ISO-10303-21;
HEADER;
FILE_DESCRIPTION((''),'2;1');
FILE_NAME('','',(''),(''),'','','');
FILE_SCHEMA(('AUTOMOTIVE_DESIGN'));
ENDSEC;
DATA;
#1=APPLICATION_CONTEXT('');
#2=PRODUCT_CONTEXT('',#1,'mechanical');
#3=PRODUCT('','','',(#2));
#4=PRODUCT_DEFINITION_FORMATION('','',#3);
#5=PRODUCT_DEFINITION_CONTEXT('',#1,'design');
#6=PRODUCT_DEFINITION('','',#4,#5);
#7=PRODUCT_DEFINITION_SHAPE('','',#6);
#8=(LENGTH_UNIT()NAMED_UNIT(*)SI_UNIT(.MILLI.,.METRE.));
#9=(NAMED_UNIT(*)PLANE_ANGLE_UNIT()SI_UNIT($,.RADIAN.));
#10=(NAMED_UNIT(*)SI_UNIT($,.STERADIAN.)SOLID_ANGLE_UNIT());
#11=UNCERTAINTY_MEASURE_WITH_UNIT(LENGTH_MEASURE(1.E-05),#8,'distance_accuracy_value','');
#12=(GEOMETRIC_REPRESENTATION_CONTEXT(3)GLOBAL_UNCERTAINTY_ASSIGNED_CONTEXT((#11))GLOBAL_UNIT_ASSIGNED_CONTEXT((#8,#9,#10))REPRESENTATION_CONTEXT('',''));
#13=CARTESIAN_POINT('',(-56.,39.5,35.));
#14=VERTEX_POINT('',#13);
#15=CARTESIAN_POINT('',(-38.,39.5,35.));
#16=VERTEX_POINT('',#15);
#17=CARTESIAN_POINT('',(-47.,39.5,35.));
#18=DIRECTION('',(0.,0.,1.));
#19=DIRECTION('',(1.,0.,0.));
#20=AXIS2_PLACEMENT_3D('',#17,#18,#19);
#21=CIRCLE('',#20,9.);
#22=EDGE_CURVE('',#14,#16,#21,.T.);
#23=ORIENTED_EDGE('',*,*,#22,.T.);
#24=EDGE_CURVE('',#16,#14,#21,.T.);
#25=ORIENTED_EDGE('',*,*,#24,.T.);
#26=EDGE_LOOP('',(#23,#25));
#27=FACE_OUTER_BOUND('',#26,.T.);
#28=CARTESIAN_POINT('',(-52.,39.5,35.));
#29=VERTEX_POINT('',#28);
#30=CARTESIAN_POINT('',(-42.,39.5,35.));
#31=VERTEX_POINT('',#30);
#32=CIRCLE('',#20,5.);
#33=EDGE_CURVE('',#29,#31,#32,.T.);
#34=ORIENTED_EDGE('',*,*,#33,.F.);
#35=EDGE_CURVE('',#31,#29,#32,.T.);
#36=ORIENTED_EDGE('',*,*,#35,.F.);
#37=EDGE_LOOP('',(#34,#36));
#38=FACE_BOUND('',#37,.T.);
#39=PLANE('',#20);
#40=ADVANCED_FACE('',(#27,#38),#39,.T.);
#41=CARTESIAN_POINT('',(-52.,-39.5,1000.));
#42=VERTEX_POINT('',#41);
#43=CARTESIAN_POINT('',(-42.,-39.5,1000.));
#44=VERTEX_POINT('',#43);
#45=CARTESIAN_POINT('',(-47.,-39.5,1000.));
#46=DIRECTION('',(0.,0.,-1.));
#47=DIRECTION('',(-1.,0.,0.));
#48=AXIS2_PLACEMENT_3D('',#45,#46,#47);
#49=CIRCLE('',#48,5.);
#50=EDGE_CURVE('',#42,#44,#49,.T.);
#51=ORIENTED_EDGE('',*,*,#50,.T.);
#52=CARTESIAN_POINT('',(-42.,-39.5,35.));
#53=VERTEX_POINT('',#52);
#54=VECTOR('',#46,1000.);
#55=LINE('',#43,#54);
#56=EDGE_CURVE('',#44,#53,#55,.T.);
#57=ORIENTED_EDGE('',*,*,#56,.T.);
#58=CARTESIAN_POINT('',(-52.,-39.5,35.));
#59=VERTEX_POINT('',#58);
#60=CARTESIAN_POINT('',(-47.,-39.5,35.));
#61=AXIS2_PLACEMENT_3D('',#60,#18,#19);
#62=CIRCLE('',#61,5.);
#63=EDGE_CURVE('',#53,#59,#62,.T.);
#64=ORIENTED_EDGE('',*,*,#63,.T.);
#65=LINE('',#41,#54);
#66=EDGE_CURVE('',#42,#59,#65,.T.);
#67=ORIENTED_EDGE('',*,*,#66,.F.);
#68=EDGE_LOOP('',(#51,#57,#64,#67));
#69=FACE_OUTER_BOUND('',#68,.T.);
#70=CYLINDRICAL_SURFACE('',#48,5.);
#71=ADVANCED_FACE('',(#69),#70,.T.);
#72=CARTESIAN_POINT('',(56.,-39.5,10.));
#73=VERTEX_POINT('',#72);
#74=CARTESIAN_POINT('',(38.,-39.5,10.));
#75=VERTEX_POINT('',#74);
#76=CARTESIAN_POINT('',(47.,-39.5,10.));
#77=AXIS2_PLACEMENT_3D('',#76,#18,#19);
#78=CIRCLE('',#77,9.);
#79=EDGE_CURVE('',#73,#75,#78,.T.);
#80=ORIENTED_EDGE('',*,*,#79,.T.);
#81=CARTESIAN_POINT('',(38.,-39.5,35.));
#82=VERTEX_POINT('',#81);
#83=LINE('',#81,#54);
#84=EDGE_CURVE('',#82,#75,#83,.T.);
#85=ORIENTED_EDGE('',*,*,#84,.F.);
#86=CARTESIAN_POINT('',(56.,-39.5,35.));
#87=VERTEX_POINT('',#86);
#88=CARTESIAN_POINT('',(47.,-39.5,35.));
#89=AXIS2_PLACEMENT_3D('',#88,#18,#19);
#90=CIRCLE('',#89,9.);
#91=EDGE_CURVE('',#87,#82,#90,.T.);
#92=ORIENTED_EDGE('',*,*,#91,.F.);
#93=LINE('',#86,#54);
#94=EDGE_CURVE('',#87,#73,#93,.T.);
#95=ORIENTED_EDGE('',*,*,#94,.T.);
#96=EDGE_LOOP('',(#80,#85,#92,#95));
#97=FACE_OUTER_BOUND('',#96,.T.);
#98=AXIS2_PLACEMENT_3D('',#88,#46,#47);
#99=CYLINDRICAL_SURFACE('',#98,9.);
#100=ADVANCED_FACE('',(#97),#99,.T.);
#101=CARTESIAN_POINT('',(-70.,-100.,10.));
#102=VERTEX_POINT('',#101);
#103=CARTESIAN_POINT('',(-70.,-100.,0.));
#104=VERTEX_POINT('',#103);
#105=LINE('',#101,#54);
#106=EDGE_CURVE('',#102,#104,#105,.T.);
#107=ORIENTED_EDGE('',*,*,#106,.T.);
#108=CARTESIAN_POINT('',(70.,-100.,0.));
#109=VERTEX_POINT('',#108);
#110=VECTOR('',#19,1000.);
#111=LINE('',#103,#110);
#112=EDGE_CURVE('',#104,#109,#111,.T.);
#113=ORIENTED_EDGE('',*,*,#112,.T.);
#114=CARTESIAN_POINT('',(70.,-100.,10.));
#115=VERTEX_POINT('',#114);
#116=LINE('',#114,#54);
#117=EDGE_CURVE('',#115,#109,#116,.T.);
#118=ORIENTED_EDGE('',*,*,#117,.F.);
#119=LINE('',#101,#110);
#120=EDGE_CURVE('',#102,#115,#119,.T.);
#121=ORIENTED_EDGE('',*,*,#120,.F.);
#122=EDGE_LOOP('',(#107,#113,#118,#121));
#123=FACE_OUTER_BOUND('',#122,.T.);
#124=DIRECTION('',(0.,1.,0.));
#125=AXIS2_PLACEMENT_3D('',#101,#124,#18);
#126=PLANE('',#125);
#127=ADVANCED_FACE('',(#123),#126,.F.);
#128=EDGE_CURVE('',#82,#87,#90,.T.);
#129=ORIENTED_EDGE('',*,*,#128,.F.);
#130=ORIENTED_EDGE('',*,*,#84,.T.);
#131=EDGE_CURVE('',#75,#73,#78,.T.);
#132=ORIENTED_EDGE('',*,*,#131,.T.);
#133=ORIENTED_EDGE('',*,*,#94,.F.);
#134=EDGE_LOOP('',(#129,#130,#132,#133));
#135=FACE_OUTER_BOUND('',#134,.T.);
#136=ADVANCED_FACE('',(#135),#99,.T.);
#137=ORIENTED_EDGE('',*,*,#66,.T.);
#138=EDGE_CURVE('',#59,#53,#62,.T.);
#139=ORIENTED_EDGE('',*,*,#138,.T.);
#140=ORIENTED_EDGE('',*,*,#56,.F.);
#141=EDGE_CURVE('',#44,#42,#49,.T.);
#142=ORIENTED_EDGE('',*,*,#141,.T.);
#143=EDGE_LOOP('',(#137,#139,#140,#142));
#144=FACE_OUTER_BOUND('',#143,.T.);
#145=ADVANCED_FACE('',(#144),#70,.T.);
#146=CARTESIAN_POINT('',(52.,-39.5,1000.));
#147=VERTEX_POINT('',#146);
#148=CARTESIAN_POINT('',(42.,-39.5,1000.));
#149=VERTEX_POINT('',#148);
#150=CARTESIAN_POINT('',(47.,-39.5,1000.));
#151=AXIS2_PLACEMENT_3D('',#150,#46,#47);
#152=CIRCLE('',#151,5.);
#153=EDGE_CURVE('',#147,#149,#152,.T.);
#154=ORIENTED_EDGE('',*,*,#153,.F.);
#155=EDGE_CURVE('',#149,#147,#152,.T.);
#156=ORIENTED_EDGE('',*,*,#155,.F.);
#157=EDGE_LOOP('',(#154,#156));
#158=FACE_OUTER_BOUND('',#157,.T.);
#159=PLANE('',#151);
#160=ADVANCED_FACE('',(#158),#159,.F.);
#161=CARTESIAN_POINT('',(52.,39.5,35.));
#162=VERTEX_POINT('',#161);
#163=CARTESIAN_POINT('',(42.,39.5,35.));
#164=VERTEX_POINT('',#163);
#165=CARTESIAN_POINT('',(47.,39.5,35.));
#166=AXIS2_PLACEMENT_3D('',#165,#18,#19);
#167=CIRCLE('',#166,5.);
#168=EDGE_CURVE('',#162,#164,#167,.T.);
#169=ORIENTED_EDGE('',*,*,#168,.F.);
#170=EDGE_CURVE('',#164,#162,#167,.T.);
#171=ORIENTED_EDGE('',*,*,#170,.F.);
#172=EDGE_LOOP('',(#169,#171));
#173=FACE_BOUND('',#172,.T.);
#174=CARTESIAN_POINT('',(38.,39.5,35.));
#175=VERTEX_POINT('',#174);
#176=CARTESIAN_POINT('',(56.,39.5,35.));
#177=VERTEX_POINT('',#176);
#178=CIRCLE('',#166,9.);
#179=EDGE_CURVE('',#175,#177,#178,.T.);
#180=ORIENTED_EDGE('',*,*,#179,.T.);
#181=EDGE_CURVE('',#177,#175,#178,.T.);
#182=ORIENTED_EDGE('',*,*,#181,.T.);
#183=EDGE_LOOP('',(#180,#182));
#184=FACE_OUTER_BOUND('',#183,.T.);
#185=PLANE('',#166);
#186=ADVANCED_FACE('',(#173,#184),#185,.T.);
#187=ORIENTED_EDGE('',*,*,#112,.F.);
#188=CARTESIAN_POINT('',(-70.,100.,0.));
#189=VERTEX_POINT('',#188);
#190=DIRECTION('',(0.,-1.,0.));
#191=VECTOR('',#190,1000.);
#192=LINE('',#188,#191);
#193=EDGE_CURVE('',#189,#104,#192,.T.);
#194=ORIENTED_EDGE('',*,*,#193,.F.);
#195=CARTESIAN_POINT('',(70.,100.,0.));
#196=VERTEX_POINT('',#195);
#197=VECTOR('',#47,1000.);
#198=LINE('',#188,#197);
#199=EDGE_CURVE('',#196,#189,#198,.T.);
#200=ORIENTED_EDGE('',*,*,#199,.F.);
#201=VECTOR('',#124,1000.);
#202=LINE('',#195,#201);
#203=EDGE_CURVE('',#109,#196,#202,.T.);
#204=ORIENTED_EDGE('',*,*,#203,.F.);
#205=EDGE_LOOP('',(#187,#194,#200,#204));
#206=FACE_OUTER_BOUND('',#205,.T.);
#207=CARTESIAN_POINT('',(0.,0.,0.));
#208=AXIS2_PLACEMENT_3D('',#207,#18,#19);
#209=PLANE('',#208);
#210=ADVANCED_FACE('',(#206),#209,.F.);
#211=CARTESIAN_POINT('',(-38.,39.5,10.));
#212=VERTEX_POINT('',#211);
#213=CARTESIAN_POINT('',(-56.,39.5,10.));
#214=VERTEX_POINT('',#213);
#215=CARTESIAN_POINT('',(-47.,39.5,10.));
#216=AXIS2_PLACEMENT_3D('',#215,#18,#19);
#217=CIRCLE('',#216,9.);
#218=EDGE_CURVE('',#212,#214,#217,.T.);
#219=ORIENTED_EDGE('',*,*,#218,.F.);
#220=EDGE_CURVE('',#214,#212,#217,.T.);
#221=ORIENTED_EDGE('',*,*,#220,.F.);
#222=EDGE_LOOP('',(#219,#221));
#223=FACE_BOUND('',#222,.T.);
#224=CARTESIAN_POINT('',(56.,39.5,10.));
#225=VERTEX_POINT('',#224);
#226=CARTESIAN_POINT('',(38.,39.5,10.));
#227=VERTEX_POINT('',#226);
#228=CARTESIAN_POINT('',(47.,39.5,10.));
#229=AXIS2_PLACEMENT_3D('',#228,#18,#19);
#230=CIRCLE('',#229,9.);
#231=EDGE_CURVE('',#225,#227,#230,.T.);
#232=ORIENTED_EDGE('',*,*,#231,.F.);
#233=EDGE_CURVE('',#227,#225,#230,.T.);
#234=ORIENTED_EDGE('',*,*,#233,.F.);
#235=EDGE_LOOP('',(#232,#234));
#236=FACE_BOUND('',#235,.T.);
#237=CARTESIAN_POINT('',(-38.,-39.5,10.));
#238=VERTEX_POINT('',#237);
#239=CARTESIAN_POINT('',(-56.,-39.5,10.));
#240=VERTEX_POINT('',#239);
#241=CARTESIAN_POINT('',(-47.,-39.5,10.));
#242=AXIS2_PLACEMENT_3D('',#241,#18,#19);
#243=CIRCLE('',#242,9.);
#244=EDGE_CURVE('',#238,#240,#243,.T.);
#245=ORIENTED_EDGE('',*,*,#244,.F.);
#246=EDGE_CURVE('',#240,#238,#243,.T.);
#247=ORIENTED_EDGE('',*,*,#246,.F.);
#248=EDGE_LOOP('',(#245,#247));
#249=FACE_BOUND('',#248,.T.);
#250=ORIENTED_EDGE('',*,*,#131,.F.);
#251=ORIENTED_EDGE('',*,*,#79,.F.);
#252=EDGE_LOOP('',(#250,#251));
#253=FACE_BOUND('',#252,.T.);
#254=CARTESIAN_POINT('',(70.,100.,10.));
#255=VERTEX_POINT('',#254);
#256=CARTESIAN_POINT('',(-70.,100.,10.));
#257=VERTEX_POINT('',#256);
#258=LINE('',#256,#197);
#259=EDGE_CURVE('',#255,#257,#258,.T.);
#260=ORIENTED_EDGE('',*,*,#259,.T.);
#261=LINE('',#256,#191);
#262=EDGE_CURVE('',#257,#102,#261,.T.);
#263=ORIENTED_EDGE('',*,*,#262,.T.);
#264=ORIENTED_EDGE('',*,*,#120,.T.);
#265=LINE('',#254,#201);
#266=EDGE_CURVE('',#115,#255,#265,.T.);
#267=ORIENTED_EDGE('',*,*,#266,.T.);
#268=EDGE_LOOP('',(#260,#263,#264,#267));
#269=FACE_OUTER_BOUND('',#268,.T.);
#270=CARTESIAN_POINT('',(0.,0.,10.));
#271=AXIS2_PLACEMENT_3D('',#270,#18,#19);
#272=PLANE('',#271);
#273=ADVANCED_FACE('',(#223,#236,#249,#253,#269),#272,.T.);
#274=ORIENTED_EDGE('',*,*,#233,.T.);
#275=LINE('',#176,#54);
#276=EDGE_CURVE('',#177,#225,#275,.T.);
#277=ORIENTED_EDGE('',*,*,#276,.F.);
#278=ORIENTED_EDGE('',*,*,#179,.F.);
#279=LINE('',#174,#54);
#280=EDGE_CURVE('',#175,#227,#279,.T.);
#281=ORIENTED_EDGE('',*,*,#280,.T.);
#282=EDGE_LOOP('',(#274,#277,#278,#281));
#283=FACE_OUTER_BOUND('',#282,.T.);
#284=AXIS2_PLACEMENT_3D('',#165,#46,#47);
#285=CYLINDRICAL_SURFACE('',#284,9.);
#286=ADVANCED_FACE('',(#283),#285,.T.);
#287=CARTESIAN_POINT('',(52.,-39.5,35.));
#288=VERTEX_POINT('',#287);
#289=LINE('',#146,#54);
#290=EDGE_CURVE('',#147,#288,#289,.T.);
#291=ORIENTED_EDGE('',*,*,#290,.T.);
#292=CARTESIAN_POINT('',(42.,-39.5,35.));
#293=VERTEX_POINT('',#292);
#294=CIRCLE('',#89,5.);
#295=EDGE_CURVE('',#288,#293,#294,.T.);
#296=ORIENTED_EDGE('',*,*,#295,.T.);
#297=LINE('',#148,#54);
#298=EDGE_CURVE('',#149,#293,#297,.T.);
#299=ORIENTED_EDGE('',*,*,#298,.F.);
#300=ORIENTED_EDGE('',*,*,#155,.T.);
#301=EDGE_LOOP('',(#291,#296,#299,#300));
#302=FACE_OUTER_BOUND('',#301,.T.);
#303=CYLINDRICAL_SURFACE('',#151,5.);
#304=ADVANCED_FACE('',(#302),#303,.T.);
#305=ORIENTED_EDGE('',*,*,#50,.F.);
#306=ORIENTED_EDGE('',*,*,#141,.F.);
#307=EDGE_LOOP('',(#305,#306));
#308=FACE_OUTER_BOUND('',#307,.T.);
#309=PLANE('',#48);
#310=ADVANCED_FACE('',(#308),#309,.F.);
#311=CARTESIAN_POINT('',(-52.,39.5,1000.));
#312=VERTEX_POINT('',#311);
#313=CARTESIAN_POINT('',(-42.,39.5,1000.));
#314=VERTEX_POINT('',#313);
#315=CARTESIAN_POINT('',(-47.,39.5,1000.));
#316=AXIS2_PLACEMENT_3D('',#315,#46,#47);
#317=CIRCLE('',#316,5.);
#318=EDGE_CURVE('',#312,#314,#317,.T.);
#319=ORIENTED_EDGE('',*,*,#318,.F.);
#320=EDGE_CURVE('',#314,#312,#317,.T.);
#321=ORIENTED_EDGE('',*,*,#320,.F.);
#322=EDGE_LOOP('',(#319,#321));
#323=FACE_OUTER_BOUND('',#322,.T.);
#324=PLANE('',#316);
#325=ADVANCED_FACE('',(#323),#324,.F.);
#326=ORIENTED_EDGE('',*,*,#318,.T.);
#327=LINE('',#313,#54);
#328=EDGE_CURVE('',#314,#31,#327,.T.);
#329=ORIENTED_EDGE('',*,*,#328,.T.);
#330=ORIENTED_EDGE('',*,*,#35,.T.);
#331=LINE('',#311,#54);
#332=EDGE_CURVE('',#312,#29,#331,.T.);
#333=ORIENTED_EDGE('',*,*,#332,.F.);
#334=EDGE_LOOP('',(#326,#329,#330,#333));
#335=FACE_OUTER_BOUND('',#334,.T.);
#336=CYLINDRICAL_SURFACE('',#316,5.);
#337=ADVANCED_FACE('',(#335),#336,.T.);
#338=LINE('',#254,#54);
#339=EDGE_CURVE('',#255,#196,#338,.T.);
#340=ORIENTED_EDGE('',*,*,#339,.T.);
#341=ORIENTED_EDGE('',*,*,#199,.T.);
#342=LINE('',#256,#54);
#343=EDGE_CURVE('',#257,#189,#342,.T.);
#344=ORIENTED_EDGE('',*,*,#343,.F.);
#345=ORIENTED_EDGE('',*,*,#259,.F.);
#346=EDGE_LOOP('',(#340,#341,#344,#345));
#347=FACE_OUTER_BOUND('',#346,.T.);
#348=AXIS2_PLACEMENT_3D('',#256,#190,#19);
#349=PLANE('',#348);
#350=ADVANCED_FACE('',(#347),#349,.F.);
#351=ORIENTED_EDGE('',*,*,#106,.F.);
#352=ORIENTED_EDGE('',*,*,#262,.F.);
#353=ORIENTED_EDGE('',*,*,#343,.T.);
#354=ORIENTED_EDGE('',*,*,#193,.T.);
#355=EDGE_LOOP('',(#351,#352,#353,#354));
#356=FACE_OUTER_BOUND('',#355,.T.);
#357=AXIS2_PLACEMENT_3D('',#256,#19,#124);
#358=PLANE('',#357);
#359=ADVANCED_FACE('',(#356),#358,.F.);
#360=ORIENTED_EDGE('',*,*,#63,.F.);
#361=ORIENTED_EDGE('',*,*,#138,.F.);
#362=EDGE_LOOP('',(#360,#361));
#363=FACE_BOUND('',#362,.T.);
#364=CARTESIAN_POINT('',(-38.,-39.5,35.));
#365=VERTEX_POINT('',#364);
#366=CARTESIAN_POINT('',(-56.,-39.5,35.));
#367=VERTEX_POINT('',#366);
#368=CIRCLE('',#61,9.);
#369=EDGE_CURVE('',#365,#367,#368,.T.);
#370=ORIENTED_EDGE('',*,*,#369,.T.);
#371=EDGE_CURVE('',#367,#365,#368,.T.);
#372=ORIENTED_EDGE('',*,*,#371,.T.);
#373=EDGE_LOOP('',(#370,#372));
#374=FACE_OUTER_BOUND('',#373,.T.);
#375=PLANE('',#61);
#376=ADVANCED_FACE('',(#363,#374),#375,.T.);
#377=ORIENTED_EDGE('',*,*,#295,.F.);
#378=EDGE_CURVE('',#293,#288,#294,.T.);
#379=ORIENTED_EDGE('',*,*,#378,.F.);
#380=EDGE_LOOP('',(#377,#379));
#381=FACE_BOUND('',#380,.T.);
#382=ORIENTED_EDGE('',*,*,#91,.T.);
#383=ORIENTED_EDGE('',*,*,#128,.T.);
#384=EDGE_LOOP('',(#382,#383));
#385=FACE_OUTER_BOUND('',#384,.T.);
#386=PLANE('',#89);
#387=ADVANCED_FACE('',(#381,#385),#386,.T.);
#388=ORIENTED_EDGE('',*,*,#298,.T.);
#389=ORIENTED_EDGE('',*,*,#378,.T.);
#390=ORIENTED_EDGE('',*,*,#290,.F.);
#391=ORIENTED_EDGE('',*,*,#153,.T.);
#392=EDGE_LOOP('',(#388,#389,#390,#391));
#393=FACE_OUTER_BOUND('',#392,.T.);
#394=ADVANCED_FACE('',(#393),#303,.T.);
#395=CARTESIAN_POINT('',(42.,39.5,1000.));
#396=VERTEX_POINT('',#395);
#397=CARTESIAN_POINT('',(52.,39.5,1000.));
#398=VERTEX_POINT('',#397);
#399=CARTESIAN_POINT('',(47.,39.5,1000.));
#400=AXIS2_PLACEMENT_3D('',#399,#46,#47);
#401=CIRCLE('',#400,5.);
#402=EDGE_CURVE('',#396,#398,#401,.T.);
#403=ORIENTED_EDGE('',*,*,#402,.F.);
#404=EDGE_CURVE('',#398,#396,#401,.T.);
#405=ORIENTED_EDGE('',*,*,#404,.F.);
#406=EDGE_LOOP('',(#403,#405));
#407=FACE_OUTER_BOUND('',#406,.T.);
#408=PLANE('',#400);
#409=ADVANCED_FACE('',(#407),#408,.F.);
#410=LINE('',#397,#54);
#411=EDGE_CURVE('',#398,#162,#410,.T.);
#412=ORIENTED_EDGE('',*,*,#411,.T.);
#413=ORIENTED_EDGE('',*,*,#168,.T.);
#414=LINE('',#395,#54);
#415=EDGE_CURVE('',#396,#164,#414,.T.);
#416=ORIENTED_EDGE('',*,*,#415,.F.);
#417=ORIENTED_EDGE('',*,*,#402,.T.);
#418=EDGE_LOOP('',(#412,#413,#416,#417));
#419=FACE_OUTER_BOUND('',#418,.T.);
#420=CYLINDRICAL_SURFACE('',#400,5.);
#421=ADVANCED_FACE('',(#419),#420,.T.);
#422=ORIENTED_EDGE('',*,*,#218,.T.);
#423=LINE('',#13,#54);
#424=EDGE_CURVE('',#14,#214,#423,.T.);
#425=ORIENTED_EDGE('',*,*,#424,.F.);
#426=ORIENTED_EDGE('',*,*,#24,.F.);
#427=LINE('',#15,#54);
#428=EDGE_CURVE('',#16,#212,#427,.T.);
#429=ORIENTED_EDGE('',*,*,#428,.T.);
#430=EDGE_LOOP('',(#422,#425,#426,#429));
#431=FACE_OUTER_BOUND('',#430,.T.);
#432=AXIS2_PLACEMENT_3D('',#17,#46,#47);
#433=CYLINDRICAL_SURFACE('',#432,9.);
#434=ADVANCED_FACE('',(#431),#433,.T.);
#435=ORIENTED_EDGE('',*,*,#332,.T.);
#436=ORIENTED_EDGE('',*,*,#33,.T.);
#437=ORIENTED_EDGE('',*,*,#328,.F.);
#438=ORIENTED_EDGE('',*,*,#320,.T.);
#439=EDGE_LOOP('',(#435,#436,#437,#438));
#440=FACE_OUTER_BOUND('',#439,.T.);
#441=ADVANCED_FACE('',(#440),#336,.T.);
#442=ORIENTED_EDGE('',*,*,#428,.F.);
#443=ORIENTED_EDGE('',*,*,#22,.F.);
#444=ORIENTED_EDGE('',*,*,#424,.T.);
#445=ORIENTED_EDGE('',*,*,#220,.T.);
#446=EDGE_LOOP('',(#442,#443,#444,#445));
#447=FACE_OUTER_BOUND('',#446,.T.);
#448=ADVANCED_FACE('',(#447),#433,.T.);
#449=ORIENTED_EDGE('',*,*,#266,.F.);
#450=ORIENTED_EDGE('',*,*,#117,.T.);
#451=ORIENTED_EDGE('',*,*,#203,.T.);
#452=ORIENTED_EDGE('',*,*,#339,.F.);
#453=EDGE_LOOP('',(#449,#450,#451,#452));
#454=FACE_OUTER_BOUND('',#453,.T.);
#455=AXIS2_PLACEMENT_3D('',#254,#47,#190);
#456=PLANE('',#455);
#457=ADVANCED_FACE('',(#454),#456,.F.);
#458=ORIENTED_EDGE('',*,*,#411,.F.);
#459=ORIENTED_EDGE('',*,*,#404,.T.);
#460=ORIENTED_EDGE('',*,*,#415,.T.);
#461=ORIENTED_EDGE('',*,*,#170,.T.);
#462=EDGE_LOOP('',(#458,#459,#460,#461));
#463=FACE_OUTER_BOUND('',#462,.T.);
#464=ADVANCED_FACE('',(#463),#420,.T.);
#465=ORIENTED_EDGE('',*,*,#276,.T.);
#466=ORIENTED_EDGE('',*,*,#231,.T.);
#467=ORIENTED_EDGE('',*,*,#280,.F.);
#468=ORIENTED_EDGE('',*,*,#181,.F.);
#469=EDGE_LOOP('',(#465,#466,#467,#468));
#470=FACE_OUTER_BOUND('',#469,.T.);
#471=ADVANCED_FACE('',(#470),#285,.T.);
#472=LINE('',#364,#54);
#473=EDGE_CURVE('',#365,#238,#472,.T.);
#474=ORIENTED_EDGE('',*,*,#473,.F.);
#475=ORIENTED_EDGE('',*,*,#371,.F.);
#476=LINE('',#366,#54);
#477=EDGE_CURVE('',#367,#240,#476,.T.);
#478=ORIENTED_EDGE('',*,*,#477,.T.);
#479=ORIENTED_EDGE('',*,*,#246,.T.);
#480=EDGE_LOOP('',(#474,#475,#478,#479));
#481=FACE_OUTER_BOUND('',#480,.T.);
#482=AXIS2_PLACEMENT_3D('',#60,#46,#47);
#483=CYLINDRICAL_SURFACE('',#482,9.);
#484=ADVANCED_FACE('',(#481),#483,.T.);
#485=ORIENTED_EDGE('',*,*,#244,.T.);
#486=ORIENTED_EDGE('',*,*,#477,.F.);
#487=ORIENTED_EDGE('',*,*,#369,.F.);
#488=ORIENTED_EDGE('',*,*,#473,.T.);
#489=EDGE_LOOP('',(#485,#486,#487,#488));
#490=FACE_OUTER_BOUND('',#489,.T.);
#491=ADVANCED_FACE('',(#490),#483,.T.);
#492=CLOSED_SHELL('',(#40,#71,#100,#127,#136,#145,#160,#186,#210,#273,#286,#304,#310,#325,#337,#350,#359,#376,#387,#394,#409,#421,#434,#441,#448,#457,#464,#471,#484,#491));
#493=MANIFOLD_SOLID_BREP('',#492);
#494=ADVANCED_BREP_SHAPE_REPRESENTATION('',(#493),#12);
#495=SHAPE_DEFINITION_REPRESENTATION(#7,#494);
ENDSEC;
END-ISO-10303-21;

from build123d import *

# Parameters (mm, degrees)
SKETCH2_W           = 140
SKETCH2_H           = 200
SKETCH2_R           = 5
BOSS_EXTRUDE1_DEPTH = 10
SKETCH3_R           = 9
SKETCH3_R_2         = 5
BOSS_EXTRUDE2_DEPTH = 25
SKETCH4_R           = 5
BOSS_EXTRUDE3_DEPTH = 1000


with BuildPart() as part:
    # Sketch2 → Boss-Extrude1 (new body)
    with BuildSketch(Plane.XY):
        Rectangle(SKETCH2_W, SKETCH2_H)
        with Locations((-47, 39.5)):
            Circle(SKETCH2_R, mode=Mode.SUBTRACT)
        with Locations((-47, -39.5)):
            Circle(SKETCH2_R, mode=Mode.SUBTRACT)
        with Locations((47, 39.5)):
            Circle(SKETCH2_R, mode=Mode.SUBTRACT)
        with Locations((47, -39.5)):
            Circle(SKETCH2_R, mode=Mode.SUBTRACT)
    extrude(amount=BOSS_EXTRUDE1_DEPTH)

    # Sketch3 → Boss-Extrude2 (add)
    # profile 1 of 4: a face of its own
    with BuildSketch(Plane.XY.offset(10)):
        with Locations((-47, 39.5)):
            Circle(SKETCH3_R)
        with Locations((-47, 39.5)):
            Circle(SKETCH3_R_2, mode=Mode.SUBTRACT)
    # profile 2 of 4: a face of its own
    with BuildSketch(Plane.XY.offset(10)):
        with Locations((47, 39.5)):
            Circle(SKETCH3_R)
        with Locations((47, 39.5)):
            Circle(SKETCH3_R_2, mode=Mode.SUBTRACT)
    # profile 3 of 4: a face of its own
    with BuildSketch(Plane.XY.offset(10)):
        with Locations((47, -39.5)):
            Circle(SKETCH3_R)
        with Locations((47, -39.5)):
            Circle(SKETCH3_R_2, mode=Mode.SUBTRACT)
    # profile 4 of 4: a face of its own
    with BuildSketch(Plane.XY.offset(10)):
        with Locations((-47, -39.5)):
            Circle(SKETCH3_R)
        with Locations((-47, -39.5)):
            Circle(SKETCH3_R_2, mode=Mode.SUBTRACT)
    extrude(amount=BOSS_EXTRUDE2_DEPTH)

    # Sketch4 → Boss-Extrude3 (add)
    with BuildSketch(Plane(origin=(0, 0, 0), x_dir=(-1, 0, 0), z_dir=(0, 0, -1))):
        with Locations((-47, 39.5)):
            Circle(SKETCH4_R)
        with Locations((47, 39.5)):
            Circle(SKETCH4_R)
        with Locations((47, -39.5)):
            Circle(SKETCH4_R)
        with Locations((-47, -39.5)):
            Circle(SKETCH4_R)
    extrude(amount=-BOSS_EXTRUDE3_DEPTH)


solid = part.part
